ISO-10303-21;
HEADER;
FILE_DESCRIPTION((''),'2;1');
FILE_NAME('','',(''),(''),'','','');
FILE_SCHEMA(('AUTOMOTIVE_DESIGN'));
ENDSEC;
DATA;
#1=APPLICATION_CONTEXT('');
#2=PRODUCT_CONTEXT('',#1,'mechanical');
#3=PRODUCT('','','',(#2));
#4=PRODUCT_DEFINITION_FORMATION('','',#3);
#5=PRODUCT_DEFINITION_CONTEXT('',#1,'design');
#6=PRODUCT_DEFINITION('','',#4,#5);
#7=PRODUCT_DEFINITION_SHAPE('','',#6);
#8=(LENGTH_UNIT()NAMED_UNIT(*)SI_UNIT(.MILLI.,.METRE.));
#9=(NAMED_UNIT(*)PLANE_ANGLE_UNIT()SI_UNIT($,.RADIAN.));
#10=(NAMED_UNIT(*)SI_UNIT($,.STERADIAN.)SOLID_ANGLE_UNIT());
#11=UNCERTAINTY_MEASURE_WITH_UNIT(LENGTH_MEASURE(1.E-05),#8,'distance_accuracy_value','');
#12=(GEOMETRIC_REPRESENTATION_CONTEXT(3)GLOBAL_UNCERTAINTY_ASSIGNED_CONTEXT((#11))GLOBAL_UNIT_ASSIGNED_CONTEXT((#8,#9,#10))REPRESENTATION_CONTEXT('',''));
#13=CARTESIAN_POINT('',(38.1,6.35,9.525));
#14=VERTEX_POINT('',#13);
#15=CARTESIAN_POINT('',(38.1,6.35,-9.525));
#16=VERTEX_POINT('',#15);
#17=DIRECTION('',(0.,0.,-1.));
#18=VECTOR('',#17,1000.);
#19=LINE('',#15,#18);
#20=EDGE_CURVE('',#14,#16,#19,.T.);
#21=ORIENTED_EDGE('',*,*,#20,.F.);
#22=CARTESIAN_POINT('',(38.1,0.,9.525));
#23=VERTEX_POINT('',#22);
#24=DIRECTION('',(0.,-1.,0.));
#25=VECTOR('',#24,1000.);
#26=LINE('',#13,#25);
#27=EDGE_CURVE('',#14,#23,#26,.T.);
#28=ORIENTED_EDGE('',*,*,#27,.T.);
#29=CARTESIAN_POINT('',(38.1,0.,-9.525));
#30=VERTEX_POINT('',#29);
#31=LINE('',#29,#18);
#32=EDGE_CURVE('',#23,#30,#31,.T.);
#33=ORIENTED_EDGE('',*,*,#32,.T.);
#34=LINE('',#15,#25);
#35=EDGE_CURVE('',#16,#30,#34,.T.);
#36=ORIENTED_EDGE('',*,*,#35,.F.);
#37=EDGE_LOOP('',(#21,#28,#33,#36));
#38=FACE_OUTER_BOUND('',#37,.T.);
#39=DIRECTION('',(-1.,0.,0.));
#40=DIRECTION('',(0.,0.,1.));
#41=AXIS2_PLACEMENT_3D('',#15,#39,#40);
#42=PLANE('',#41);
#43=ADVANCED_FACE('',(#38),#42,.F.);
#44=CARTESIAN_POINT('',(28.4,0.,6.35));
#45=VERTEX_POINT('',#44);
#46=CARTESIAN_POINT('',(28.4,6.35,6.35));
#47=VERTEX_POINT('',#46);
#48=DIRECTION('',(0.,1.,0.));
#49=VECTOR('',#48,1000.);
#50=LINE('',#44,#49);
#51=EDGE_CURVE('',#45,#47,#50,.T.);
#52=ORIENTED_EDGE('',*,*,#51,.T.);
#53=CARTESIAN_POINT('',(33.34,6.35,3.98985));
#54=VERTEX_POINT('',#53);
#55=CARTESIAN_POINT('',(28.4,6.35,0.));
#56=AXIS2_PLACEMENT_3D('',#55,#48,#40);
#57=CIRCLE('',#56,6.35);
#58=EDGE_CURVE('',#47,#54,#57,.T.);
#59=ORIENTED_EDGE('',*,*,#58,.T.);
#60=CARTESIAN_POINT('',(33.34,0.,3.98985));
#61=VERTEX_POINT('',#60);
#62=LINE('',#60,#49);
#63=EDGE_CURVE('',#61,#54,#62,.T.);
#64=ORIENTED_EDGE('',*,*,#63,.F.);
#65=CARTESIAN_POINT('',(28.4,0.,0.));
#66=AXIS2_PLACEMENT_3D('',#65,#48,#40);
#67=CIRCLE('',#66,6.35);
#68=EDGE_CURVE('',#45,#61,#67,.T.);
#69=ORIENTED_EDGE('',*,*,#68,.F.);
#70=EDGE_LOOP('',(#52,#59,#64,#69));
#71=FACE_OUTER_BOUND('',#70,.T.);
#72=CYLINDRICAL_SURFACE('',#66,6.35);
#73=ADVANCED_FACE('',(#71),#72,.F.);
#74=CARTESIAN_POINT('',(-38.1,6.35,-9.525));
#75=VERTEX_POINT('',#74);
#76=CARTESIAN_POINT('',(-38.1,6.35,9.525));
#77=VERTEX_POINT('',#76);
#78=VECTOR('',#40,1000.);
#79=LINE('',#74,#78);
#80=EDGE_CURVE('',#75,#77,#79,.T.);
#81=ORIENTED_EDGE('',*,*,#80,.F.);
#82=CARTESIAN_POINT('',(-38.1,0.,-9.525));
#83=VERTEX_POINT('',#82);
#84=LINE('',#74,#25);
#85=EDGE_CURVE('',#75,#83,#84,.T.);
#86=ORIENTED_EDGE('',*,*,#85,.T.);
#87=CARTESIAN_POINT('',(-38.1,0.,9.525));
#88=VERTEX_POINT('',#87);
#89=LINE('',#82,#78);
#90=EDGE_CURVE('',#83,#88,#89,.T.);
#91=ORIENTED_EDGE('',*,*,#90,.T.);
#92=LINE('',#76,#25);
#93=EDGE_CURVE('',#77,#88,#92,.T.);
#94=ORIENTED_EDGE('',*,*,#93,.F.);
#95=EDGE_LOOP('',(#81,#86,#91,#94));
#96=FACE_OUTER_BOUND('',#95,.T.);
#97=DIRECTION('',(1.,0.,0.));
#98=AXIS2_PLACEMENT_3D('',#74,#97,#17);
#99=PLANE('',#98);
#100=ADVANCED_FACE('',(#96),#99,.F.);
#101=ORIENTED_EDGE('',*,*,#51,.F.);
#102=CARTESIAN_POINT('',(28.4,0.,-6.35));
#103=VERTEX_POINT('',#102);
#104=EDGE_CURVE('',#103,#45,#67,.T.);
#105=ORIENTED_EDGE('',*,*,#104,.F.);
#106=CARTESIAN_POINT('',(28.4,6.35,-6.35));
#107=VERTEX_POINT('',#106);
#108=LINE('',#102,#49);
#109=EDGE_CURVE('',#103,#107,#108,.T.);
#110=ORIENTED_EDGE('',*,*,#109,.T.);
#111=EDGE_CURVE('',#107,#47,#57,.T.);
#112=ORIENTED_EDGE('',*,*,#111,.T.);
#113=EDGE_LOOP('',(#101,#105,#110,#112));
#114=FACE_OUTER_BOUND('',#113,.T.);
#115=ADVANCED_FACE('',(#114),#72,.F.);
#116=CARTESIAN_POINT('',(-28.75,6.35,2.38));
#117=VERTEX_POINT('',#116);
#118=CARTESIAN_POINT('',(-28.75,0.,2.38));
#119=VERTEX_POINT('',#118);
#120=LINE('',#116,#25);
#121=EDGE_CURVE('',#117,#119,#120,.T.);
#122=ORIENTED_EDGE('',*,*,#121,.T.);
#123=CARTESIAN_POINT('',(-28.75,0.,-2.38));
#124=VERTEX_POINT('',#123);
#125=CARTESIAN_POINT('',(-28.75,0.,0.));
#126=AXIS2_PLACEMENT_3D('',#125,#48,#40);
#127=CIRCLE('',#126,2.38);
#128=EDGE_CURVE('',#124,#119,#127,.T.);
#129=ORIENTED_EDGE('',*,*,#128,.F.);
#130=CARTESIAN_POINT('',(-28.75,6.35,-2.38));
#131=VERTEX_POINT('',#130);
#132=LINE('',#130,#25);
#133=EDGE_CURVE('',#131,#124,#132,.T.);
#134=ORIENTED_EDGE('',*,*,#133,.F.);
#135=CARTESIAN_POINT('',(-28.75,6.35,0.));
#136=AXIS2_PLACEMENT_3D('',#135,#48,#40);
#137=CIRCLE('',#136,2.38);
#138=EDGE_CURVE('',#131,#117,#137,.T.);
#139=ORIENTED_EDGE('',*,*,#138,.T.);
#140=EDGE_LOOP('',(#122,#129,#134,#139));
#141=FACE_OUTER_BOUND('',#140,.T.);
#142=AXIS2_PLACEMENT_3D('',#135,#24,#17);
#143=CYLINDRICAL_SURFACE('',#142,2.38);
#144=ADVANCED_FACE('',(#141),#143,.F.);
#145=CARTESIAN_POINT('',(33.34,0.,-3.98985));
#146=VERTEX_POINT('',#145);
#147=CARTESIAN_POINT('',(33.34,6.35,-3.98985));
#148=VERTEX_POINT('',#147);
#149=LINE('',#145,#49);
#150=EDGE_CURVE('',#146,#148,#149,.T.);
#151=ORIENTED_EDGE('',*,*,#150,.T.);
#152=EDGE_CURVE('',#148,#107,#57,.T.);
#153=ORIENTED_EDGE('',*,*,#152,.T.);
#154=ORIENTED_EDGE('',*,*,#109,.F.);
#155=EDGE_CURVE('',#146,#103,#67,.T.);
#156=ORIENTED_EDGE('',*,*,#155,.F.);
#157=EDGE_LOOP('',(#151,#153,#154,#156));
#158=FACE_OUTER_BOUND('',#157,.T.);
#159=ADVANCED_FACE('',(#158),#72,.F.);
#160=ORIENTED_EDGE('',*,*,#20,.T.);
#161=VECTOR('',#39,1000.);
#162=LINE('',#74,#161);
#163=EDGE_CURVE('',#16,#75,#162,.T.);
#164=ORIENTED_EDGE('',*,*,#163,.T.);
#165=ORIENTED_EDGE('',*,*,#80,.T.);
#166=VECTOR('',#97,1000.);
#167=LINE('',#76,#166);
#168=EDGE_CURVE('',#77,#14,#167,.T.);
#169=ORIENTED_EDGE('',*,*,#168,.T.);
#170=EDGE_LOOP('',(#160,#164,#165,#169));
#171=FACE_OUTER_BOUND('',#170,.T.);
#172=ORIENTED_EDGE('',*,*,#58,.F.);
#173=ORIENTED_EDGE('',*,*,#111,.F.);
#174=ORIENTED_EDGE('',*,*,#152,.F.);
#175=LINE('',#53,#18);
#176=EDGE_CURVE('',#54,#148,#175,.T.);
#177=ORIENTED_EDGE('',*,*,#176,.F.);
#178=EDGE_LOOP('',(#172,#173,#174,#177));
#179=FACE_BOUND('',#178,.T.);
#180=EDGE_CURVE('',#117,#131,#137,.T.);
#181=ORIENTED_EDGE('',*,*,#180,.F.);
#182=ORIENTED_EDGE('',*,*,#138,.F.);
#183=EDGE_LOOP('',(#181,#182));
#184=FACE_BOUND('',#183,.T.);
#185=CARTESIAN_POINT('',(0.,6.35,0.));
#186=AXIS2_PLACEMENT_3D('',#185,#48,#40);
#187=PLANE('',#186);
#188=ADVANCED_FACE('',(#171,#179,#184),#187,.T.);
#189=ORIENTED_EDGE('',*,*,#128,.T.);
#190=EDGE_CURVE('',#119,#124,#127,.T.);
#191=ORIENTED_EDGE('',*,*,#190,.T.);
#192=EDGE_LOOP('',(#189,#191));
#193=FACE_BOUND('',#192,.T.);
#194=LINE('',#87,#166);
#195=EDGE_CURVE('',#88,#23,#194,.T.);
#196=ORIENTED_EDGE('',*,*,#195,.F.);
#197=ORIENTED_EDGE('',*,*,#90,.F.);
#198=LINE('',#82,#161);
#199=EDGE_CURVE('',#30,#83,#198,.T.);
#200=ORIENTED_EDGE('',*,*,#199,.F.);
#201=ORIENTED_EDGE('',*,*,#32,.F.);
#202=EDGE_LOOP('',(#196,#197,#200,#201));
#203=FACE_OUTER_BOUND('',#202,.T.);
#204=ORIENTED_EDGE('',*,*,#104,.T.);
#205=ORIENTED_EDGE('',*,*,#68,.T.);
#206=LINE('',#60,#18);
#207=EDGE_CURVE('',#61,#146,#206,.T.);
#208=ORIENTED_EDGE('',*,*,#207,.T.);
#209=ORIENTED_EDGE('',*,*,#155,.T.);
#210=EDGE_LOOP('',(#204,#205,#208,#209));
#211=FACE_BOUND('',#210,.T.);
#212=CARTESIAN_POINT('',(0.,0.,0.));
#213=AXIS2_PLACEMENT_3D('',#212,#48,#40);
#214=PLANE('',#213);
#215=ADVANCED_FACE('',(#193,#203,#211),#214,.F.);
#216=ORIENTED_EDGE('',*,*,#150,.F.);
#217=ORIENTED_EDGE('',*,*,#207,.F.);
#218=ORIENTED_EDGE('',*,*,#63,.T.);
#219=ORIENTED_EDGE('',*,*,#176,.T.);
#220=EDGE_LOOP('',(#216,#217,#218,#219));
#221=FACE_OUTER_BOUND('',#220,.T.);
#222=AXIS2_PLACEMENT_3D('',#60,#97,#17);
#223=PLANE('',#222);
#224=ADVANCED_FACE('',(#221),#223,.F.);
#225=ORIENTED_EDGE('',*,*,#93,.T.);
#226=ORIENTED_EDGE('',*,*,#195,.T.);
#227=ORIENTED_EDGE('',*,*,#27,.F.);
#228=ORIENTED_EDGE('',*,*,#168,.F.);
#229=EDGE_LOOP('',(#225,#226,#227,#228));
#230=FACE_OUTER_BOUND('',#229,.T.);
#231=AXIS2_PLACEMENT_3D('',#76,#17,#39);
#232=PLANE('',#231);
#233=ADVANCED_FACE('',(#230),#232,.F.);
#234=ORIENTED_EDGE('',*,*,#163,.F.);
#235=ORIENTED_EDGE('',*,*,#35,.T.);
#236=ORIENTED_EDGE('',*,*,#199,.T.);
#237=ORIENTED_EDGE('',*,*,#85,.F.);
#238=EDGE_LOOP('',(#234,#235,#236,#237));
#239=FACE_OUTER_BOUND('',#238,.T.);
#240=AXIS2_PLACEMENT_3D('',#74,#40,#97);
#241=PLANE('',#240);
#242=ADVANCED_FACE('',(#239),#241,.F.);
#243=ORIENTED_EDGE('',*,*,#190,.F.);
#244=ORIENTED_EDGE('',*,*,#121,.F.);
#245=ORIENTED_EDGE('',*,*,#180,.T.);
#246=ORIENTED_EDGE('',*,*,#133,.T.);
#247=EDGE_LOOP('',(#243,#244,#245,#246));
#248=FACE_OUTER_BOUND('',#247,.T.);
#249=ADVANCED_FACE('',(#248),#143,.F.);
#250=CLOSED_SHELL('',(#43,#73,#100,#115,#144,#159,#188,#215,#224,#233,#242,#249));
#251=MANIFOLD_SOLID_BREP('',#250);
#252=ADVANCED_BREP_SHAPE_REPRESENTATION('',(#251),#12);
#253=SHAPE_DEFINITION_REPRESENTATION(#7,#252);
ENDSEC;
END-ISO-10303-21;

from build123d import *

# Parameters (mm, degrees)
BAR_OUTLINE_AND_HOLE_4_76_SKETCH_W = 76.2
BAR_OUTLINE_AND_HOLE_4_76_SKETCH_H = 19.05
BAR_OUTLINE_AND_HOLE_4_76_SKETCH_R = 2.38
LINK_BAR_6_35_THICK_DEPTH          = 6.35
D_HOLE_12_7_CUT_DEPTH              = 6.35


with BuildPart() as part:
    # Bar Outline and Hole Ø4.76 Sketch → Link Bar 6.35 Thick (new body)
    with BuildSketch(Plane(origin=(0, 0, 0), x_dir=(1, 0, 0), z_dir=(0, 1, 0))):
        Rectangle(BAR_OUTLINE_AND_HOLE_4_76_SKETCH_W, BAR_OUTLINE_AND_HOLE_4_76_SKETCH_H)
        with Locations(Location((-28.75, 0, 0), (0, 0, 270))):
            Circle(BAR_OUTLINE_AND_HOLE_4_76_SKETCH_R, mode=Mode.SUBTRACT)
    extrude(amount=LINK_BAR_6_35_THICK_DEPTH)

    # D-Hole Ø12.7 Sketch → D-Hole Ø12.7 Cut (cut)
    with BuildSketch(Plane(origin=(0, 6.35, 0), x_dir=(1, 0, 0), z_dir=(0, 1, 0))):
        with BuildLine():
            Line((33.34, -3.989849621), (33.34, 3.989849621))
            ThreePointArc((33.34, 3.989849621), (22.05, 0), (33.34, -3.989849621))
        make_face()
    extrude(amount=-D_HOLE_12_7_CUT_DEPTH, mode=Mode.SUBTRACT)


solid = part.part
